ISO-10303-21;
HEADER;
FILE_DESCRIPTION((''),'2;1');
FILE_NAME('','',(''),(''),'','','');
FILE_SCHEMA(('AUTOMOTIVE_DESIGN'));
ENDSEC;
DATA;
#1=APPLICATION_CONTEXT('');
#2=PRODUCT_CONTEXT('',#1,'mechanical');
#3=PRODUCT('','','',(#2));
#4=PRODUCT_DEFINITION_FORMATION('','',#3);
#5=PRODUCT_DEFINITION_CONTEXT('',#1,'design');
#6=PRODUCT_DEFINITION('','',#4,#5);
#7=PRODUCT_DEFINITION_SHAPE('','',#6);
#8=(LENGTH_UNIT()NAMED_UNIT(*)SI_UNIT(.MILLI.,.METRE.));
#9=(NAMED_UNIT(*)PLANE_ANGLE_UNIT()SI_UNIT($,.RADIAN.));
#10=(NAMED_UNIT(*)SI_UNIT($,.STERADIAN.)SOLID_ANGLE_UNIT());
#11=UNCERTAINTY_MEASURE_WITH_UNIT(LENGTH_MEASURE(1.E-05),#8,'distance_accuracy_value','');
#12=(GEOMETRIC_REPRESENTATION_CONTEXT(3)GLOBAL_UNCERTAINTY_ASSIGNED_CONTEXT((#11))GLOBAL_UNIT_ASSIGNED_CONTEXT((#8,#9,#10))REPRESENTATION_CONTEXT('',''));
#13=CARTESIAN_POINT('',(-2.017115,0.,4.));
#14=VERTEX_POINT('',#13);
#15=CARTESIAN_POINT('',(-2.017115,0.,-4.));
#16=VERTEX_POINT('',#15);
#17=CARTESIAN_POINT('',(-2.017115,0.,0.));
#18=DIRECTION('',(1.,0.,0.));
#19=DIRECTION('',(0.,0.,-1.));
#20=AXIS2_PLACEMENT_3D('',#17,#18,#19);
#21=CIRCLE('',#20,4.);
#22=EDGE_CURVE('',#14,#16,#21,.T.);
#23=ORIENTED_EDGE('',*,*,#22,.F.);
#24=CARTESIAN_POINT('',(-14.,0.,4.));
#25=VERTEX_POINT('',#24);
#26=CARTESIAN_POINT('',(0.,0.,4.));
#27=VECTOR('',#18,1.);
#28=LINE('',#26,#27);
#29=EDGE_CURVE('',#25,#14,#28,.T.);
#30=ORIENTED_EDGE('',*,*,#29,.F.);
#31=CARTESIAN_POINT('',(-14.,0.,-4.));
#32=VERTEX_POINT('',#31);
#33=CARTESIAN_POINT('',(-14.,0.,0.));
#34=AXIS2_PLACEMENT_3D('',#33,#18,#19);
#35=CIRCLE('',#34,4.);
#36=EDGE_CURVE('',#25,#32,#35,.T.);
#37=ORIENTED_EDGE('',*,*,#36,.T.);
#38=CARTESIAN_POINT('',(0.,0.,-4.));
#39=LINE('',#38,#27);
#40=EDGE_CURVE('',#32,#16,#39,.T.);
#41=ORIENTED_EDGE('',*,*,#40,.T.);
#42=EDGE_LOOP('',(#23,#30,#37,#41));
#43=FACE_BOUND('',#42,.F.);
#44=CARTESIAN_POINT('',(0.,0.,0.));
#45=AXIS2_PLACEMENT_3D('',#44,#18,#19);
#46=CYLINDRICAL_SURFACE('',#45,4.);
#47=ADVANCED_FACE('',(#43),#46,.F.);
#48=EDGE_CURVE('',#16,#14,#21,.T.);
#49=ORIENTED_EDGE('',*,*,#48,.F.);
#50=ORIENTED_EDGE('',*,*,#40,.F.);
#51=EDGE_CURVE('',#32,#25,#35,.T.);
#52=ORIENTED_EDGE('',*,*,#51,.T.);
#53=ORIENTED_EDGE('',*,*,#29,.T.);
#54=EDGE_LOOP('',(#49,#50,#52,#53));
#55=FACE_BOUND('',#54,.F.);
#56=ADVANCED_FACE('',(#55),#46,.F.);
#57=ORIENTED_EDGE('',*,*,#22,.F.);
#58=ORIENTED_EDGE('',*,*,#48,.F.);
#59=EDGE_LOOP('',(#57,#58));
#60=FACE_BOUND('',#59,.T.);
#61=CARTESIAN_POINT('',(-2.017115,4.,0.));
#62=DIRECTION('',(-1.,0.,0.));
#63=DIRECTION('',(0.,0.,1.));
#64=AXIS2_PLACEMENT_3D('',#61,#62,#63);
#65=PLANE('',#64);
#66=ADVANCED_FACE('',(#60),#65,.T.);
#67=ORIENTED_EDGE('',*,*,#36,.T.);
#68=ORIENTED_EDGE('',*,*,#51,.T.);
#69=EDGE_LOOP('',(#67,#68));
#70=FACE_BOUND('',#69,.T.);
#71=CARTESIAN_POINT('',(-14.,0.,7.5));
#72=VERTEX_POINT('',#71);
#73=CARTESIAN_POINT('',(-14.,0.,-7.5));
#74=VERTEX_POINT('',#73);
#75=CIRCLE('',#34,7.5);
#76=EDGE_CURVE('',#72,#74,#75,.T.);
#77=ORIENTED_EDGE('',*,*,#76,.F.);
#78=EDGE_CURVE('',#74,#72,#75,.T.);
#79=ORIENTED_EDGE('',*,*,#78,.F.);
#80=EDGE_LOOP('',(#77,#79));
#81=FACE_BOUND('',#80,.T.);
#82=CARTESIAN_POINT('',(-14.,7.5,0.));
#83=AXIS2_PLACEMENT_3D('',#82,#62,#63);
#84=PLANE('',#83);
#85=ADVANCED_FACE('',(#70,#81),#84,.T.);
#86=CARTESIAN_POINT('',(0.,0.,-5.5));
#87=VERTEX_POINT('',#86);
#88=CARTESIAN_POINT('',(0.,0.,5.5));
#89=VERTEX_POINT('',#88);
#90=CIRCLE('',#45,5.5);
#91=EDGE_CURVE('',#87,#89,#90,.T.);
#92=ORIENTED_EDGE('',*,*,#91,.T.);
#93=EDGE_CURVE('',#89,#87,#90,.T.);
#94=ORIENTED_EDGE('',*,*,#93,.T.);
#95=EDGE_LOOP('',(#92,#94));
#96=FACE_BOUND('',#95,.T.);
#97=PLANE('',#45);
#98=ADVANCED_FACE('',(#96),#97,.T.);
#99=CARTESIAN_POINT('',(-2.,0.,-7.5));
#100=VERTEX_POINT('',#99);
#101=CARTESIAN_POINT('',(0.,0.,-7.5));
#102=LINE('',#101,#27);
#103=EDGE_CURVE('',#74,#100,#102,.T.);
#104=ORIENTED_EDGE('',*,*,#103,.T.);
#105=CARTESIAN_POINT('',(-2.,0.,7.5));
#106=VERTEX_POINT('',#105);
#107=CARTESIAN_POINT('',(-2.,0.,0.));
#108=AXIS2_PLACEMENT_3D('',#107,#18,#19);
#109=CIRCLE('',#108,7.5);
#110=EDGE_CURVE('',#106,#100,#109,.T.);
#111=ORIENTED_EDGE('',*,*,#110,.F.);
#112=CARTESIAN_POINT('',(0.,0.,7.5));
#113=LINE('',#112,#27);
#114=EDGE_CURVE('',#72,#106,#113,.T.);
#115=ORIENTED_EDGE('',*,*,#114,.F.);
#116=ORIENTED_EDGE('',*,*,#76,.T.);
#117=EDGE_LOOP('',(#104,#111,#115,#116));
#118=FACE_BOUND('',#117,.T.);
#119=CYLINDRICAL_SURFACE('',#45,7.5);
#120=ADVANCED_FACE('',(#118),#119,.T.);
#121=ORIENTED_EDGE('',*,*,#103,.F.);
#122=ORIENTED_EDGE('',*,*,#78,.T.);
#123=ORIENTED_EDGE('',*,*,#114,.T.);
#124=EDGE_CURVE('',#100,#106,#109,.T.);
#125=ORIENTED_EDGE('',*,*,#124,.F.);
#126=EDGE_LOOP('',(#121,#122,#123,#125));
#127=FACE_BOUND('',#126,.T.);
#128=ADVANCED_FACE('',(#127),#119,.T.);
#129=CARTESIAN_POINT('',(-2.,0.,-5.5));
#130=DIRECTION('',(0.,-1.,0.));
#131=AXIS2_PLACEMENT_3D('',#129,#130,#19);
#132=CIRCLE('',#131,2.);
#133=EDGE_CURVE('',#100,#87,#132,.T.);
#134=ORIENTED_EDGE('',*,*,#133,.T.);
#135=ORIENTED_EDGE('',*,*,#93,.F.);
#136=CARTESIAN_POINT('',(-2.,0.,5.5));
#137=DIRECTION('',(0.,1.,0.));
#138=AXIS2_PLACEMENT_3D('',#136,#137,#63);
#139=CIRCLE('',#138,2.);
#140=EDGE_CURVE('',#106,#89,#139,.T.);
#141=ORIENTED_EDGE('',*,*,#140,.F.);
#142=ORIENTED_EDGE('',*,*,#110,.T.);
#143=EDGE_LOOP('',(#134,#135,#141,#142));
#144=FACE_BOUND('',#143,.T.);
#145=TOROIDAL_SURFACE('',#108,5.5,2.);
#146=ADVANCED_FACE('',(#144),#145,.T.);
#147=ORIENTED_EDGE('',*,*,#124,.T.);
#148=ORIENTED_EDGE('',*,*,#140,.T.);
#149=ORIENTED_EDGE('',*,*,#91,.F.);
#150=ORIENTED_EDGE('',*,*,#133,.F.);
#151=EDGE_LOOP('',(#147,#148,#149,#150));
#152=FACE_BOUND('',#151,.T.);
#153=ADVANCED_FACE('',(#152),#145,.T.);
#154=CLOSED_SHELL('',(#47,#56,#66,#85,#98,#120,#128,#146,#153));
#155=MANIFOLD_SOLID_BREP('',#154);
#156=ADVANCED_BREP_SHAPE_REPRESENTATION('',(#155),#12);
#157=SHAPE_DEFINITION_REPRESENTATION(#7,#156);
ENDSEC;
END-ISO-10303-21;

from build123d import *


with BuildPart() as part:
    # Sketch1 → Revolve1 (revolve)
    with BuildSketch(Plane.XY, mode=Mode.PRIVATE) as revolve1_sk:
        with BuildLine():
            Line((0, 0), (0, 5.5))
            ThreePointArc((0, 5.5), (-0.585786438, 6.914213562), (-2, 7.5))
            Line((-2, 7.5), (-14, 7.5))
            Line((-14, 7.5), (-14, 4))
            Line((-14, 4), (-2.017114914, 4))
            Line((-2.017114914, 4), (-2.017114914, 0))
            Line((-2.017114914, 0), (0, 0))
        make_face()
    revolve(revolve1_sk.sketch.rotate(Axis((0, 0, 0), (-1, 0, 0)), 90), axis=Axis((0, 0, 0), (-1, 0, 0)))


solid = part.part
